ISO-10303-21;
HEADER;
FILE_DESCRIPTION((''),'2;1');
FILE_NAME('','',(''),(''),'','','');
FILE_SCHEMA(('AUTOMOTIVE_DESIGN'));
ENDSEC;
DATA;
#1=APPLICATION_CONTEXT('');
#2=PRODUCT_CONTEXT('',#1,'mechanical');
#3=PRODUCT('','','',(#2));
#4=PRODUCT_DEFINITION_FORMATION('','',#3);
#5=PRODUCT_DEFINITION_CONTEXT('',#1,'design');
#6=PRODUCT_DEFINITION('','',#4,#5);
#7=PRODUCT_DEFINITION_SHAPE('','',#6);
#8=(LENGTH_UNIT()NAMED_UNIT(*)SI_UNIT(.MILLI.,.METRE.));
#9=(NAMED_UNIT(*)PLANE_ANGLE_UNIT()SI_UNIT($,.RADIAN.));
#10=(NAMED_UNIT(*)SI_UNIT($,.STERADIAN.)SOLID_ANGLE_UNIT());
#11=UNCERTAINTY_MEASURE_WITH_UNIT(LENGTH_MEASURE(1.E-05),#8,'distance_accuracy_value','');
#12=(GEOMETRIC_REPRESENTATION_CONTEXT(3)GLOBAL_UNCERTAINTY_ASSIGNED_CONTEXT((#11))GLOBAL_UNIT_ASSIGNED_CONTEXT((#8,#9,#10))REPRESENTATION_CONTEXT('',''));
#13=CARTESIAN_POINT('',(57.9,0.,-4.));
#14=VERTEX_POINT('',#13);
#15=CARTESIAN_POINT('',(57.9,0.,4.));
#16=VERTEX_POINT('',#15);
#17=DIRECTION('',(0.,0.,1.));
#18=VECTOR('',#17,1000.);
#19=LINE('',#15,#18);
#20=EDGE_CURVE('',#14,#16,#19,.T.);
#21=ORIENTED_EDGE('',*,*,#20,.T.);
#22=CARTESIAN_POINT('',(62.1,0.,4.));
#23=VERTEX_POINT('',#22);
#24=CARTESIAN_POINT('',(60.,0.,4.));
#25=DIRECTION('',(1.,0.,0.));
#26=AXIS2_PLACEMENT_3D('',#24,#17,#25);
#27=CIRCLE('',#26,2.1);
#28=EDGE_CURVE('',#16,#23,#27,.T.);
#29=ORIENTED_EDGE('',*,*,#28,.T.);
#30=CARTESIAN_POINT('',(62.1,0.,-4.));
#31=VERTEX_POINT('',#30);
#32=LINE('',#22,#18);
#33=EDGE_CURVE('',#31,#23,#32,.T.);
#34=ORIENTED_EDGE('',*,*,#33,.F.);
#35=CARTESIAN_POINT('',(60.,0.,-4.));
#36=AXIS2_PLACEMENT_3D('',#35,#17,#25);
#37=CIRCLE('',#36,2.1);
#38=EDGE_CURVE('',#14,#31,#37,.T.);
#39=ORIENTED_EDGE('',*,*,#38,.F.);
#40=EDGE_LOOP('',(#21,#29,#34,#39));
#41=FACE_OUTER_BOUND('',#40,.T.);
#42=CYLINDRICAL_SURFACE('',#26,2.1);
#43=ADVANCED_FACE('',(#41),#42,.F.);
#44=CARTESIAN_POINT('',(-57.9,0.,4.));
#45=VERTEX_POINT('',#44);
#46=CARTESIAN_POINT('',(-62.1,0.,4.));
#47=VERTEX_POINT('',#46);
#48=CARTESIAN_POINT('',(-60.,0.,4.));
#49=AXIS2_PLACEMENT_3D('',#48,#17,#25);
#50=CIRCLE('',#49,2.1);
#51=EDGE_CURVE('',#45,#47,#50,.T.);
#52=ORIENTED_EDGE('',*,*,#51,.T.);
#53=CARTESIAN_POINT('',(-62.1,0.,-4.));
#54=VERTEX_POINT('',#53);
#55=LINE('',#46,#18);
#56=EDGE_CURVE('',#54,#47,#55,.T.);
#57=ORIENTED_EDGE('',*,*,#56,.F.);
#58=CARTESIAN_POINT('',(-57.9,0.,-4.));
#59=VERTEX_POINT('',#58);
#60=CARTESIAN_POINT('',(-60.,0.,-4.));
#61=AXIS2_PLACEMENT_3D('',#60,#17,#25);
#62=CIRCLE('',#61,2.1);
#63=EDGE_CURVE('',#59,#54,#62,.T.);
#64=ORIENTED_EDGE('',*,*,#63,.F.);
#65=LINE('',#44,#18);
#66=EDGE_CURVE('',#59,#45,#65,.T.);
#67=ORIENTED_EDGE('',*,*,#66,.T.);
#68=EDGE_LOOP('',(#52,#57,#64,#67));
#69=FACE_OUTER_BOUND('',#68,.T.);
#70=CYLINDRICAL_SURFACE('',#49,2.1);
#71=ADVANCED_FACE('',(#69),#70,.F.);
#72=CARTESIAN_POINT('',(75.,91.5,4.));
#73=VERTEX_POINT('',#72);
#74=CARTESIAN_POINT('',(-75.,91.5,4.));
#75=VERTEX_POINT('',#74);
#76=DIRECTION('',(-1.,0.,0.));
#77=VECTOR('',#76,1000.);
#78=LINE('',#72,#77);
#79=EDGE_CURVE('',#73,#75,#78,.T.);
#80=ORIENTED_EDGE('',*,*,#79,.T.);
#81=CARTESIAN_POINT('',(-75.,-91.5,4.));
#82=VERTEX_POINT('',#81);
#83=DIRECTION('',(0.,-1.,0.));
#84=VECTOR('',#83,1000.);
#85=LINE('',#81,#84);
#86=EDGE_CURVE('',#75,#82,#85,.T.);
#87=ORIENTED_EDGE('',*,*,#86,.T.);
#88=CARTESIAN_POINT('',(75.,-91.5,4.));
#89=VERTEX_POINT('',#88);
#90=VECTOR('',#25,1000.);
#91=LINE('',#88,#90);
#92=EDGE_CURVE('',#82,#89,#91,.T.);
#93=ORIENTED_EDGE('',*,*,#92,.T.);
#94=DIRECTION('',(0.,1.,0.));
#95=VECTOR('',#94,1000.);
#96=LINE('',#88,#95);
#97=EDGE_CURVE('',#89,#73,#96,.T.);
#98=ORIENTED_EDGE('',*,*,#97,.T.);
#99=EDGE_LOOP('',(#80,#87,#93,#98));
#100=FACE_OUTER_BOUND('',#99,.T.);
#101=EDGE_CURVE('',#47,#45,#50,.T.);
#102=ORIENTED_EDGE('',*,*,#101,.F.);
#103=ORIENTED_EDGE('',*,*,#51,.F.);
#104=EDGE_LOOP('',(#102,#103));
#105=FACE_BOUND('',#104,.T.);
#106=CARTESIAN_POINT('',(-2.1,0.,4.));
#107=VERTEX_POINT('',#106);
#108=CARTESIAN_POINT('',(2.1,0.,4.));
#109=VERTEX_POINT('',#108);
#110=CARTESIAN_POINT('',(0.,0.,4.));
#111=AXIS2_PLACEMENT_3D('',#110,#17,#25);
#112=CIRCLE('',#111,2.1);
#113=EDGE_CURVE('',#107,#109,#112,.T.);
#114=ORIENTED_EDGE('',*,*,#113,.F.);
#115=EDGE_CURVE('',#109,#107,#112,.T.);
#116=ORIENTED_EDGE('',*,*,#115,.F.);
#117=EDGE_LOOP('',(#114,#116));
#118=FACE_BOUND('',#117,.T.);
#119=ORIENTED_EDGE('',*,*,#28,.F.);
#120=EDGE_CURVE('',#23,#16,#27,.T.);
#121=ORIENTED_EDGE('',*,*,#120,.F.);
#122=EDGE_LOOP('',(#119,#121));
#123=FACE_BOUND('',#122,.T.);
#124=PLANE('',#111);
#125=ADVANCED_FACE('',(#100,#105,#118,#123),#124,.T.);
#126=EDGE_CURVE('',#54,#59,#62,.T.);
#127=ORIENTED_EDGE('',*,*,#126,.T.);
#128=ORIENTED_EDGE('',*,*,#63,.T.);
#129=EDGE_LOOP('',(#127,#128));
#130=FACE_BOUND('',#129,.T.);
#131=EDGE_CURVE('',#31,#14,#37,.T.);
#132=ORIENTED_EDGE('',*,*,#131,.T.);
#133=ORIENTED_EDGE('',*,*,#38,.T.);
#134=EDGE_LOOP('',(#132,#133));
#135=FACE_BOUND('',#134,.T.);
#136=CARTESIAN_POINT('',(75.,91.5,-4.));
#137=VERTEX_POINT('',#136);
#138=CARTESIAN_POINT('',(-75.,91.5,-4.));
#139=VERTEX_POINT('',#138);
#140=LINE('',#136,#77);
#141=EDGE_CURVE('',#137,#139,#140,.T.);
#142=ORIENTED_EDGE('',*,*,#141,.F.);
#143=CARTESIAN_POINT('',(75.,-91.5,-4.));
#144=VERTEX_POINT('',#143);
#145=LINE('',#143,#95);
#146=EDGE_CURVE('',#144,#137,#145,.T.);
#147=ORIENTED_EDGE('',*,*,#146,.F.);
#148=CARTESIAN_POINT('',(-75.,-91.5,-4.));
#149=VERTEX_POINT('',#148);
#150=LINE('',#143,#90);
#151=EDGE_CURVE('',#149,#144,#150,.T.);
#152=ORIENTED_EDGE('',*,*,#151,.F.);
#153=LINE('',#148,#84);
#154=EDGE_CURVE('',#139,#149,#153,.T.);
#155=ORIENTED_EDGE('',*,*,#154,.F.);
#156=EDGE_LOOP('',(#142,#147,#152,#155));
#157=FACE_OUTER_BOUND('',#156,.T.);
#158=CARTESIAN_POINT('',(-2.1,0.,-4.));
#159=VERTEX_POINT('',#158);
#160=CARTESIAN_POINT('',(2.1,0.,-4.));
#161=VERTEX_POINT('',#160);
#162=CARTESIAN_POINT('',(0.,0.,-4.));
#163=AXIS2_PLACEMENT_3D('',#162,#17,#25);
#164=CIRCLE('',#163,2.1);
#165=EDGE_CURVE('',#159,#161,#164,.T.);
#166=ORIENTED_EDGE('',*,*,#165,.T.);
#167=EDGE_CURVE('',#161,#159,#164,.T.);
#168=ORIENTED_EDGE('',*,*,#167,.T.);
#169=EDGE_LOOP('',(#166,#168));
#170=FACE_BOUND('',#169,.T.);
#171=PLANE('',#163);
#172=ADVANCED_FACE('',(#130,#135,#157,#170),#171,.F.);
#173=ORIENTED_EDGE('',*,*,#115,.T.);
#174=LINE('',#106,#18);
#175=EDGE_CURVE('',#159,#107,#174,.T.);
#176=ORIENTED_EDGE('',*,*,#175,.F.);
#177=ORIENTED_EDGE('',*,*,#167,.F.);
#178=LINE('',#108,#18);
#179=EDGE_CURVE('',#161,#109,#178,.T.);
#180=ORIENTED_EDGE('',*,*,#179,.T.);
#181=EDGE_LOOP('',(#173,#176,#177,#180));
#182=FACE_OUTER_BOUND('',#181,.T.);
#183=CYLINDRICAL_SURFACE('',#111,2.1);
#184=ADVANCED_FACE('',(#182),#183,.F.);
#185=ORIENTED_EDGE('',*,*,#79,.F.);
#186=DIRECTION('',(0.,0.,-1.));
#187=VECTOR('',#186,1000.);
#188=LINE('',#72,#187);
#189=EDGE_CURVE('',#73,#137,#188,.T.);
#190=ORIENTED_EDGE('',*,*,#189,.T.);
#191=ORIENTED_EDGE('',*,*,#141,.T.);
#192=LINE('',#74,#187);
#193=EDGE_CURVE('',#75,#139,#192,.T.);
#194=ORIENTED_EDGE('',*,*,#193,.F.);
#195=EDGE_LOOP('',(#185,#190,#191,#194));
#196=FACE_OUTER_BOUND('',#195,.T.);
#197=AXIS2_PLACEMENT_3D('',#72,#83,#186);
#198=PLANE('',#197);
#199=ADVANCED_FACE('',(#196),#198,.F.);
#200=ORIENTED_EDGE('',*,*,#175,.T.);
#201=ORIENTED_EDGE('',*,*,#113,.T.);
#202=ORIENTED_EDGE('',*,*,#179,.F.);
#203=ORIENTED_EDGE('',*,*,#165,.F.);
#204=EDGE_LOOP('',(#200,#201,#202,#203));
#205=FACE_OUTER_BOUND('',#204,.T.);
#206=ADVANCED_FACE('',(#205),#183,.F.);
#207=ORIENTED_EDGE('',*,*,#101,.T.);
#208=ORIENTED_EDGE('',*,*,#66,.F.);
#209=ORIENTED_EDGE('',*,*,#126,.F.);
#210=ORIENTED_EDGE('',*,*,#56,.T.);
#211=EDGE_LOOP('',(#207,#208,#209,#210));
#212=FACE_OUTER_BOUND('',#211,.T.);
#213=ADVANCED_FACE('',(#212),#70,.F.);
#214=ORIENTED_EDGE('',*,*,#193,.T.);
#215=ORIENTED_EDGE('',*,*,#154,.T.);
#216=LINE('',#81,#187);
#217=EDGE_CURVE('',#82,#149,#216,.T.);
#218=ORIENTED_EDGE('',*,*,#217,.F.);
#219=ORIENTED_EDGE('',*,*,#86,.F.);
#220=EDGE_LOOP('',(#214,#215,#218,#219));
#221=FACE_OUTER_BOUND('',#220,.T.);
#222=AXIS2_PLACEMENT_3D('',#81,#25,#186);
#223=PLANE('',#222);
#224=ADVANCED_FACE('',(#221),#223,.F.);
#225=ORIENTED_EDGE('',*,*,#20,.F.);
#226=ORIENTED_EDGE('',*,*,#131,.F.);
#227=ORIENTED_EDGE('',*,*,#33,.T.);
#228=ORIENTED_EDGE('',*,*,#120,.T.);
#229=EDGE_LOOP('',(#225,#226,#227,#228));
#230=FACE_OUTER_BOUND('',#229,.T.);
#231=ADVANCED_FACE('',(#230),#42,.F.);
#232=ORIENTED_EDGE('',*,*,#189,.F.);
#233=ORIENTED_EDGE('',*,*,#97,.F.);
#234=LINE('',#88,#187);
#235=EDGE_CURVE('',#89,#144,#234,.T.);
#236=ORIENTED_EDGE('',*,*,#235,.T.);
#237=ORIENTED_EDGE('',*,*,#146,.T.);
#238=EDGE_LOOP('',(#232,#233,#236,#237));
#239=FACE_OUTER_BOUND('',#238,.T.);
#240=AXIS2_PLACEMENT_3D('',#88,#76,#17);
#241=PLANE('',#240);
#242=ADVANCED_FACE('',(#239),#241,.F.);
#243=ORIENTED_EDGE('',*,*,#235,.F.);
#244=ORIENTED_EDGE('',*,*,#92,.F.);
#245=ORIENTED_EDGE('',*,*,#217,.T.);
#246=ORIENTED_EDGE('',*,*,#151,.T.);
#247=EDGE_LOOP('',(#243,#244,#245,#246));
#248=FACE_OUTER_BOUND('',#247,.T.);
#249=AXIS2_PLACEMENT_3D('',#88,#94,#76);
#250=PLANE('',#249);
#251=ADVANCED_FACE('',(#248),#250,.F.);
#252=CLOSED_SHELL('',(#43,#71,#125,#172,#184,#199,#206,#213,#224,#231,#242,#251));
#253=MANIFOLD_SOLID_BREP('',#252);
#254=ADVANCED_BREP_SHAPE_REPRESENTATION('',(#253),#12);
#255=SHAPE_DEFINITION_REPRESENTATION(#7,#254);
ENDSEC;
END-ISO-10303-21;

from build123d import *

# Parameters (mm, degrees)
SKETCH1_W           = 150
SKETCH1_H           = 183
BOSS_EXTRUDE1_DEPTH = 4
M5_TAPPED_HOLE1_D   = 4.2


with BuildPart() as part:
    # Sketch1 → Boss-Extrude1 (new, symmetric)
    with BuildSketch(Plane.XY):
        Rectangle(SKETCH1_W, SKETCH1_H)
    extrude(amount=BOSS_EXTRUDE1_DEPTH, both=True)

    # M5 Tapped Hole1 (through all)
    with Locations(Plane.XY.offset(4)):
        with Locations((-60, 0), (0, 0), (60, 0)):
            Hole(M5_TAPPED_HOLE1_D / 2)


solid = part.part
